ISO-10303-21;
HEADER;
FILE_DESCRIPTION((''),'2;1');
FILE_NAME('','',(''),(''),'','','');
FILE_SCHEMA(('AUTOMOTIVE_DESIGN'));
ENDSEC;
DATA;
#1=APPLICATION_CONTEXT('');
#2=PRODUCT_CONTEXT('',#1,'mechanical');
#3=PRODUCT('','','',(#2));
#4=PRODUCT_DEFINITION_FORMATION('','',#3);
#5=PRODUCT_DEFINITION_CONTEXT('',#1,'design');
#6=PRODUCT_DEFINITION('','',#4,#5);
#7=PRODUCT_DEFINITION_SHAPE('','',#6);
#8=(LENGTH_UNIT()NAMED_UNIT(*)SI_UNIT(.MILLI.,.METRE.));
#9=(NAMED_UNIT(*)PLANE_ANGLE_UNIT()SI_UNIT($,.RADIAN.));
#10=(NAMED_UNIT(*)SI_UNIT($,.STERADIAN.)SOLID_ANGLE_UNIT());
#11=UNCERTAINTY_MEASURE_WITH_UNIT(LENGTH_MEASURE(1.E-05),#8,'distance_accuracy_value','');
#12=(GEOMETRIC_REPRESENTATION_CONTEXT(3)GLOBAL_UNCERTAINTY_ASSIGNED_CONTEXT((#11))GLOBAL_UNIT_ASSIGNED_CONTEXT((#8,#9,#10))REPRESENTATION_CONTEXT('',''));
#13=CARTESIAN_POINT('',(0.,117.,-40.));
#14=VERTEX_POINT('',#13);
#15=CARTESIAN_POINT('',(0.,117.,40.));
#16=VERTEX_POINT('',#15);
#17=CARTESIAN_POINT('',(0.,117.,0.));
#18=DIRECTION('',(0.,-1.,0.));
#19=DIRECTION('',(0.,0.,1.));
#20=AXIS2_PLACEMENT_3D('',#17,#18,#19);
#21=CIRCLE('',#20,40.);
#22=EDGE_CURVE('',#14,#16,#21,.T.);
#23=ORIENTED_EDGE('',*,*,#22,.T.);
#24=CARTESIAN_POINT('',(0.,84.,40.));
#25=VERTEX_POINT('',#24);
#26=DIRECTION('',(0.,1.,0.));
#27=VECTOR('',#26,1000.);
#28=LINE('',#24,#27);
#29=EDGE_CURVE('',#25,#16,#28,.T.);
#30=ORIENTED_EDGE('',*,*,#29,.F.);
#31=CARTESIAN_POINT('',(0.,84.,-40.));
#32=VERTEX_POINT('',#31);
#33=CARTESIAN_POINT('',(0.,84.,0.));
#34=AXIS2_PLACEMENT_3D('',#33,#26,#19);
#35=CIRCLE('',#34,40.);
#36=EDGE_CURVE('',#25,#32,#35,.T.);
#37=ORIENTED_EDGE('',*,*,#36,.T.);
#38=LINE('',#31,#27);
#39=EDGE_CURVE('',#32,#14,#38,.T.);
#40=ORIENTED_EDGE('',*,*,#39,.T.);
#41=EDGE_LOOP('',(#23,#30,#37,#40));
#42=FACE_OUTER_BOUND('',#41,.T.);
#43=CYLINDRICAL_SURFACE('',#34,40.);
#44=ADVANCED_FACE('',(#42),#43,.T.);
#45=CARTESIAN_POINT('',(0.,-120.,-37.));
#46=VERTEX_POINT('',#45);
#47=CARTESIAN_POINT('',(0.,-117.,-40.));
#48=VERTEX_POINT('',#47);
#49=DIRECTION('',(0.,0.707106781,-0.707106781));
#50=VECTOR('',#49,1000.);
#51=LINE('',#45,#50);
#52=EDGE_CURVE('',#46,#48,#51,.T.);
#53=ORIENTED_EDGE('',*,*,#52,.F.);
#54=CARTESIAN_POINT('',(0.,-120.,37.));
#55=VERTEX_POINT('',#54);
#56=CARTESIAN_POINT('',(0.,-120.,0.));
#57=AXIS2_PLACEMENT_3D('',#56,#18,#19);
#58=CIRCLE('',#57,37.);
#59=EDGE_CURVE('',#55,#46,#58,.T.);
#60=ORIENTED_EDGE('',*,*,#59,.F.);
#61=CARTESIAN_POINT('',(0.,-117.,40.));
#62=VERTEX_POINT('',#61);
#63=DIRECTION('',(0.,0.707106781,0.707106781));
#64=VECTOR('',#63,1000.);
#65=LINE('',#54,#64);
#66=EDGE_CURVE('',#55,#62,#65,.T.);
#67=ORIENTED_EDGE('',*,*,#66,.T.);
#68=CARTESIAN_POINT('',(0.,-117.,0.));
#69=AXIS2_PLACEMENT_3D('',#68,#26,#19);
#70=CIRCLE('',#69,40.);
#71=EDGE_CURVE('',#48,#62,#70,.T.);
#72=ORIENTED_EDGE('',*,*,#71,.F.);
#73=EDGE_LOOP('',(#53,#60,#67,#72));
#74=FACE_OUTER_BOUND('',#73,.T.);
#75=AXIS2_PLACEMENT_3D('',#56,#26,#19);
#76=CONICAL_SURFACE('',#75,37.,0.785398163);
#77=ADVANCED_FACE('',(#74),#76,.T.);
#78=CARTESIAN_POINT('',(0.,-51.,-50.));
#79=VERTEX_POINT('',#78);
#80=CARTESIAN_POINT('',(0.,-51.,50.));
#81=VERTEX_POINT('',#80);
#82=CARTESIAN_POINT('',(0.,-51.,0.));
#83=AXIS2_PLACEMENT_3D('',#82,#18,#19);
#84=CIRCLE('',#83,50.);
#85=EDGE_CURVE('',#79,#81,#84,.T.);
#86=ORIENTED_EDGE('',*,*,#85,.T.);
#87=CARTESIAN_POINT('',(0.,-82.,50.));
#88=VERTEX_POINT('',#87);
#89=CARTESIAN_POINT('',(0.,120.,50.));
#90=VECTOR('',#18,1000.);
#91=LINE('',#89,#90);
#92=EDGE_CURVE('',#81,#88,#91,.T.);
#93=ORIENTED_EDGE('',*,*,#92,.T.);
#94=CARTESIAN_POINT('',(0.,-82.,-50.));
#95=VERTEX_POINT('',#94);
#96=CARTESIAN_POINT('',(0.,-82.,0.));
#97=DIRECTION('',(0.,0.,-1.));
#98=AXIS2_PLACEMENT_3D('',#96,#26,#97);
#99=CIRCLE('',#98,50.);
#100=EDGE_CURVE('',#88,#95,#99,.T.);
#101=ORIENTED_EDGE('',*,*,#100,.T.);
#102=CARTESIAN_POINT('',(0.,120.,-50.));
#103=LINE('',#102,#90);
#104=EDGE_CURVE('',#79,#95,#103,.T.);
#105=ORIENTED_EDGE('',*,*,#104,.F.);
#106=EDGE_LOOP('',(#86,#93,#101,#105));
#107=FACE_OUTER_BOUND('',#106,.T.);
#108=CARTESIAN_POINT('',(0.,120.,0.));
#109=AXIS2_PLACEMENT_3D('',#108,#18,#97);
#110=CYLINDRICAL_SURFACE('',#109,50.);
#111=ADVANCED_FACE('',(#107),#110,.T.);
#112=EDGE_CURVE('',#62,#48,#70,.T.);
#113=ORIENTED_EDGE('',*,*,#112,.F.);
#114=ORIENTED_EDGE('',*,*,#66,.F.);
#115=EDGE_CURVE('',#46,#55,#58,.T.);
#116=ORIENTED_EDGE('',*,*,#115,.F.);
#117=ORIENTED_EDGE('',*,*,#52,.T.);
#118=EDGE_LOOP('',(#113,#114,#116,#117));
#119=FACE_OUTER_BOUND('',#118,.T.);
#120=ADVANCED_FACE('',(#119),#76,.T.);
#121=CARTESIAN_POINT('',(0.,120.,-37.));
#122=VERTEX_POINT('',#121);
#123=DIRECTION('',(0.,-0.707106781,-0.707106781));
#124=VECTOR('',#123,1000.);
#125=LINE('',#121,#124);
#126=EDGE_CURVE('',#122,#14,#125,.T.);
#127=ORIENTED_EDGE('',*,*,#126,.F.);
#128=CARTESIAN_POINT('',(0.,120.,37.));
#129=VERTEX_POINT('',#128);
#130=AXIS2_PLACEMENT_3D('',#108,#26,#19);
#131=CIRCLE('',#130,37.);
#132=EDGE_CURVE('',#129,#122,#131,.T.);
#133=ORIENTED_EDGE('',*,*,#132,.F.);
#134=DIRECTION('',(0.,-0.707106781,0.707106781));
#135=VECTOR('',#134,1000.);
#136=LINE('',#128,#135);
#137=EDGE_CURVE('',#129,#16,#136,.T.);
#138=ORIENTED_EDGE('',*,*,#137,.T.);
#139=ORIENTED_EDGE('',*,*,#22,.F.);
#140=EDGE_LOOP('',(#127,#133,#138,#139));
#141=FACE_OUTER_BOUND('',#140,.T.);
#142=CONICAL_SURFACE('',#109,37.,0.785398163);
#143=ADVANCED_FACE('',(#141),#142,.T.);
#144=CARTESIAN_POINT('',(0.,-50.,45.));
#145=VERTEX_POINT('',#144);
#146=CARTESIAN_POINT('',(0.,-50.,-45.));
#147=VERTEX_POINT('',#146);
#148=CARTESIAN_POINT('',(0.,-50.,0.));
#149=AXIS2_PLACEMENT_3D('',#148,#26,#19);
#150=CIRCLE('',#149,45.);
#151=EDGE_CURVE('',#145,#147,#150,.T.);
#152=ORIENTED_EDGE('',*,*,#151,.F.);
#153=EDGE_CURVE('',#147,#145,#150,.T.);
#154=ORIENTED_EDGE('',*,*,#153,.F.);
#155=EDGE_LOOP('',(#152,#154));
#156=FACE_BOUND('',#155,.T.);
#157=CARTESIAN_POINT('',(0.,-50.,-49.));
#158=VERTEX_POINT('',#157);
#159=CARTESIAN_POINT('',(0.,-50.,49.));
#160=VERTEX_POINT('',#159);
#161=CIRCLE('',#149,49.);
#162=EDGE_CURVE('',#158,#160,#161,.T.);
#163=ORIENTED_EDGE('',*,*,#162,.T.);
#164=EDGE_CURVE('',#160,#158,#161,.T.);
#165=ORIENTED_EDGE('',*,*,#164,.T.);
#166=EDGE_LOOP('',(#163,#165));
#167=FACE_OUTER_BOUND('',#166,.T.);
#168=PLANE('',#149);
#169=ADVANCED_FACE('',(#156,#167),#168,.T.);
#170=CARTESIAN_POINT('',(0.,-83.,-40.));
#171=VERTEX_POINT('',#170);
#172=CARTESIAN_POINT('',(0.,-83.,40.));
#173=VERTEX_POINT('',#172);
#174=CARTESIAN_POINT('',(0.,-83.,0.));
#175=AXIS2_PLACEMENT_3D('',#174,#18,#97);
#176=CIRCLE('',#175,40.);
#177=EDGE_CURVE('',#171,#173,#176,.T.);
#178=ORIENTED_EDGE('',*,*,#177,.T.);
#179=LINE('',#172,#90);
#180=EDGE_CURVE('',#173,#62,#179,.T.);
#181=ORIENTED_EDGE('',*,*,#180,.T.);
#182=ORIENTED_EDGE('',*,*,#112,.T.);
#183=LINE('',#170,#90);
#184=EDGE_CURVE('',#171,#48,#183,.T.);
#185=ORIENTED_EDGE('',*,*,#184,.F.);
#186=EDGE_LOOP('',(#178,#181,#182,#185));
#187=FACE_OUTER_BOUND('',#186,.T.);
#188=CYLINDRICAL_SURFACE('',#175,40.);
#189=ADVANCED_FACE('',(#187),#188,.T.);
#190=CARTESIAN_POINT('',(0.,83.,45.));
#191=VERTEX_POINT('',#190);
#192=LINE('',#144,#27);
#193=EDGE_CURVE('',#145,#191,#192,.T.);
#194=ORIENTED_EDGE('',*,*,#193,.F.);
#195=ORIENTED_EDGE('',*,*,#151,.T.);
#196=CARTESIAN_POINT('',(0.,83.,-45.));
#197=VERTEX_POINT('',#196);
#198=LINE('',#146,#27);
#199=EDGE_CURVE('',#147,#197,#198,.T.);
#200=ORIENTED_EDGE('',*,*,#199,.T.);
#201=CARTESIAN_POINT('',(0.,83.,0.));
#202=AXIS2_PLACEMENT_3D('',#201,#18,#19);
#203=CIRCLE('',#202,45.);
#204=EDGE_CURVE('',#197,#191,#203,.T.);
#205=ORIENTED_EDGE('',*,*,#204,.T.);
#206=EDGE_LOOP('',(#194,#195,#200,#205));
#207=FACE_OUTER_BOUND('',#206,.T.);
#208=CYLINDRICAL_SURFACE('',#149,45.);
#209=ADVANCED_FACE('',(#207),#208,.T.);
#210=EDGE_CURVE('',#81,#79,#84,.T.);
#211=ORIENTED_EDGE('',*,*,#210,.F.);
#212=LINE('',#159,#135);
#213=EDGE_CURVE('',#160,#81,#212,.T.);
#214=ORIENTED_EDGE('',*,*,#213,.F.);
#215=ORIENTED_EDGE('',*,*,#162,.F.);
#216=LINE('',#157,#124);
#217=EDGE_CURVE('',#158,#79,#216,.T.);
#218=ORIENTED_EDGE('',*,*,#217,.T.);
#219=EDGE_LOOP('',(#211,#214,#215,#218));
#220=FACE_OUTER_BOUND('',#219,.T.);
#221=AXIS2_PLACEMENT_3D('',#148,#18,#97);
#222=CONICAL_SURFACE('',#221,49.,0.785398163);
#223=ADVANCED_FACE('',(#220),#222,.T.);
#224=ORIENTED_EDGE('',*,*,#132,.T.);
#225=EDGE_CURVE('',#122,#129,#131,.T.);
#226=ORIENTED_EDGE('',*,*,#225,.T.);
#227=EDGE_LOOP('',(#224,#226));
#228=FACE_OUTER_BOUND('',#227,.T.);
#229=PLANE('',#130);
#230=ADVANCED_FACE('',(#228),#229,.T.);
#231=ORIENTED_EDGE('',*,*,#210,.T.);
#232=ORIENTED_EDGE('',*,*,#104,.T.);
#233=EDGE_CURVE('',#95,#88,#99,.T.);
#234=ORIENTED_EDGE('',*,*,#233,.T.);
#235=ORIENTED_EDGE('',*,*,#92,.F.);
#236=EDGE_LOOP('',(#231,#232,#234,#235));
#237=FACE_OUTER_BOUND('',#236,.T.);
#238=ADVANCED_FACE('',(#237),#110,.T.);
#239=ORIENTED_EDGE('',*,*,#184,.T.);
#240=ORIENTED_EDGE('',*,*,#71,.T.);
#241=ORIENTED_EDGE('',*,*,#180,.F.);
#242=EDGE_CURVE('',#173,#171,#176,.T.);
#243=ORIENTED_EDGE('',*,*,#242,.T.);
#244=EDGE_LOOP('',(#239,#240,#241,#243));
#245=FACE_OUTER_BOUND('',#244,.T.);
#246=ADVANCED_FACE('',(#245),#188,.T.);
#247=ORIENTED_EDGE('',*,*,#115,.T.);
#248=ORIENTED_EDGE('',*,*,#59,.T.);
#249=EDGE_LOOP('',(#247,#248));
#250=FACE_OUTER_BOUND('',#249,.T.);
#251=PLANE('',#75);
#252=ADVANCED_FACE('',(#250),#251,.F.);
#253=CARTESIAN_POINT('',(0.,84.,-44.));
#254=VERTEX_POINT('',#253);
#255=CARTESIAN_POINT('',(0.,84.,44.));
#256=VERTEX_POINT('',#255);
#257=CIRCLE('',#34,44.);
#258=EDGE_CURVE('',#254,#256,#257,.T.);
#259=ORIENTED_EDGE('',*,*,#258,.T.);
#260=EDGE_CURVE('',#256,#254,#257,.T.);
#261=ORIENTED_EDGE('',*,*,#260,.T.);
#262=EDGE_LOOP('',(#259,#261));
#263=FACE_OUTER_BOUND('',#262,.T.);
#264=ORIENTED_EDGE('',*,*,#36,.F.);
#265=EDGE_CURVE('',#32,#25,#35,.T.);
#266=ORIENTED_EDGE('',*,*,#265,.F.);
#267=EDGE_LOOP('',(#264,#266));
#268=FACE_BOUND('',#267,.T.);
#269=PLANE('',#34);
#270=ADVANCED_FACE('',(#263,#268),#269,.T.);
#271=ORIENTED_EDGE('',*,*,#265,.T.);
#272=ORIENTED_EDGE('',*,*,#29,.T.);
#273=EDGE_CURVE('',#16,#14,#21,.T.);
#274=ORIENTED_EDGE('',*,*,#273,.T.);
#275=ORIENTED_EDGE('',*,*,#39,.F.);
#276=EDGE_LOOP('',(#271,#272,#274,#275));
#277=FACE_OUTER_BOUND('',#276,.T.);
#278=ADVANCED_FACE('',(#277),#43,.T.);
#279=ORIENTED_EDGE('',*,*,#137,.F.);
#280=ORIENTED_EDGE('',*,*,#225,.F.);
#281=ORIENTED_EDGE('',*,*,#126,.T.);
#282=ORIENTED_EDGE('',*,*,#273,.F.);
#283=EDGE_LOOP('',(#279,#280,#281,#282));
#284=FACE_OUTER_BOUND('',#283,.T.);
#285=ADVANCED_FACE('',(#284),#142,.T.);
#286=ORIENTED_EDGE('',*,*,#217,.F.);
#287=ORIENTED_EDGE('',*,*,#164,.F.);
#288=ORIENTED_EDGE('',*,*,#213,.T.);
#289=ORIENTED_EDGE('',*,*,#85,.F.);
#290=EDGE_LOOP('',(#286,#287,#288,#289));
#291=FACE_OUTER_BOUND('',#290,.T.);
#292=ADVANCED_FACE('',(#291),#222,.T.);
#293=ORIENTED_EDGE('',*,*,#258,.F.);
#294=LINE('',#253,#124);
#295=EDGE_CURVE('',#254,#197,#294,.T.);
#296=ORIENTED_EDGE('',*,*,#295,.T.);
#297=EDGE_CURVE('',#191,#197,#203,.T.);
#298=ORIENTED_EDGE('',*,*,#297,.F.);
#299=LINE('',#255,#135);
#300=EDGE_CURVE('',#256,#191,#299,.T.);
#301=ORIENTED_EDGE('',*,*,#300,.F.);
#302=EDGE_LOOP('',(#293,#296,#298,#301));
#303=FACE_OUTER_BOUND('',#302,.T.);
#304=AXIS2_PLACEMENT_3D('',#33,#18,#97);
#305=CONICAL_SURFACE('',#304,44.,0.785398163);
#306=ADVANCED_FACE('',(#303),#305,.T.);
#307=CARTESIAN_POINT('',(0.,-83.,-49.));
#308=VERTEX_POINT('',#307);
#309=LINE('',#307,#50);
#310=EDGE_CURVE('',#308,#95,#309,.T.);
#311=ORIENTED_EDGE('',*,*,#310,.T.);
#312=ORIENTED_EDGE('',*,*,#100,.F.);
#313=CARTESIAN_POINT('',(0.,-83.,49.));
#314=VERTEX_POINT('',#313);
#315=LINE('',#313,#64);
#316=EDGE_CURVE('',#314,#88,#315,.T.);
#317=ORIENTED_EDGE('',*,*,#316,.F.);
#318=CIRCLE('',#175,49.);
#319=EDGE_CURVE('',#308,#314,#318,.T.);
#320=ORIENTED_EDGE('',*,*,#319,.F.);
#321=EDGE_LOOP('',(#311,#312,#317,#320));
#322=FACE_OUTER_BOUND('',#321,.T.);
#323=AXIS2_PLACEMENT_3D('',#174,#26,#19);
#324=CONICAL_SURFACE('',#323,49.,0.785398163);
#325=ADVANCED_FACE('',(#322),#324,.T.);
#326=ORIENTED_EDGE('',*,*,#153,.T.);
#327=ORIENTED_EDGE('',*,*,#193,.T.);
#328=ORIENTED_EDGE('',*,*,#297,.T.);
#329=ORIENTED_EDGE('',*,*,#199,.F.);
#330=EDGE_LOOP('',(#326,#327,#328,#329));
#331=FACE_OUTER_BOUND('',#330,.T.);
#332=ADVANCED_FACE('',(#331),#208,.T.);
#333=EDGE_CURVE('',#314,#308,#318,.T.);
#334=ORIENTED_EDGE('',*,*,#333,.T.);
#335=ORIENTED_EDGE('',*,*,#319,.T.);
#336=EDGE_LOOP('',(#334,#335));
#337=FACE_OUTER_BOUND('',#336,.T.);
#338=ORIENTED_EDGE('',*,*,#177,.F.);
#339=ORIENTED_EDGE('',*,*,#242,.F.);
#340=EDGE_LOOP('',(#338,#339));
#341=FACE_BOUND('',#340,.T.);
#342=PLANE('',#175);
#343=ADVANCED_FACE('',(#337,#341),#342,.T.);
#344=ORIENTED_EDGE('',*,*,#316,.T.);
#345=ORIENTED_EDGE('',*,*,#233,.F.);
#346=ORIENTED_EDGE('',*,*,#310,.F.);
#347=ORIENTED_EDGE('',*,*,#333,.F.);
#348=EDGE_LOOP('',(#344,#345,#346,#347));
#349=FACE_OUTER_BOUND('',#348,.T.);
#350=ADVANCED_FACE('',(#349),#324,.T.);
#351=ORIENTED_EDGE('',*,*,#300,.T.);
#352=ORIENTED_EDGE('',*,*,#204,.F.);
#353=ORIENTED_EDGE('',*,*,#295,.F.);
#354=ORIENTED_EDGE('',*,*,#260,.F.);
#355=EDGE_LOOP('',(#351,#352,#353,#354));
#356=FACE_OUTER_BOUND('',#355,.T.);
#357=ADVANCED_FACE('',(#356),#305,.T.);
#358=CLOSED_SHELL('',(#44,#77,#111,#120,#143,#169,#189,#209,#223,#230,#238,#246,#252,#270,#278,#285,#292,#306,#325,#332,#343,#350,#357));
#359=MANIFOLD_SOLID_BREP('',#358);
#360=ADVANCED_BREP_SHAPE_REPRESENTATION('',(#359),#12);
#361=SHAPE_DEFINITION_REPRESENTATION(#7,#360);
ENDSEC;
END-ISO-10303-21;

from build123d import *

# Parameters (mm, degrees)
SKETCH1_R           = 50
BOSS_EXTRUDE1_DEPTH = 120
SKETCH2_R           = 50
SKETCH2_R_2         = 40
CUT_EXTRUDE1_DEPTH  = 36
CUT_EXTRUDE2_START  = -37
SKETCH3_R           = 50
SKETCH3_R_2         = 40
CUT_EXTRUDE2_DEPTH  = 37
SKETCH4_R           = 50
SKETCH4_R_2         = 45
CUT_EXTRUDE3_DEPTH  = 134
CHAMFER1_SIZE       = 3
CHAMFER2_SIZE       = 1


with BuildPart() as part:
    # Sketch1 → Boss-Extrude1 (new, symmetric)
    with BuildSketch(Plane(origin=(0, 0, 0), x_dir=(1, 0, 0), z_dir=(0, 1, 0))):
        with Locations(Location((0, 0, 0), (0, 0, 270))):
            Circle(SKETCH1_R)
    extrude(amount=BOSS_EXTRUDE1_DEPTH, both=True)

    # Sketch2 → Cut-Extrude1 (cut)
    with BuildSketch(Plane(origin=(0, 120, 0), x_dir=(1, 0, 0), z_dir=(0, 1, 0))):
        with Locations(Location((0, 0, 0), (0, 0, 270))):
            Circle(SKETCH2_R)
        with Locations(Location((0, 0, 0), (0, 0, 270))):
            Circle(SKETCH2_R_2, mode=Mode.SUBTRACT)
    extrude(amount=-CUT_EXTRUDE1_DEPTH, mode=Mode.SUBTRACT)

    # Sketch3 → Cut-Extrude2 (cut)
    with BuildSketch(Plane.XZ.offset(120).offset(CUT_EXTRUDE2_START)):
        with Locations(Location((0, 0, 0), (0, 0, 270))):
            Circle(SKETCH3_R)
        with Locations(Location((0, 0, 0), (0, 0, 90))):
            Circle(SKETCH3_R_2, mode=Mode.SUBTRACT)
    extrude(amount=CUT_EXTRUDE2_DEPTH, mode=Mode.SUBTRACT)

    # Sketch4 → Cut-Extrude3 (cut)
    with BuildSketch(Plane(origin=(0, 84, 0), x_dir=(1, 0, 0), z_dir=(0, 1, 0))):
        with Locations(Location((0, 0, 0), (0, 0, 90))):
            Circle(SKETCH4_R)
        with Locations(Location((0, 0, 0), (0, 0, 270))):
            Circle(SKETCH4_R_2, mode=Mode.SUBTRACT)
    extrude(amount=-CUT_EXTRUDE3_DEPTH, mode=Mode.SUBTRACT)

    # Chamfer1
    chamfer1_edges = [part.edges().sort_by_distance(p)[0] for p in [
        (0, -120, -40),
        (0, 120, -40),
    ]]
    chamfer(chamfer1_edges, length=CHAMFER1_SIZE)

    # Chamfer2
    chamfer2_edges = [part.edges().sort_by_distance(p)[0] for p in [
        (0, -83, -50),
        (0, -50, -50),
        (0, 84, -45),
    ]]
    chamfer(chamfer2_edges, length=CHAMFER2_SIZE)


solid = part.part
